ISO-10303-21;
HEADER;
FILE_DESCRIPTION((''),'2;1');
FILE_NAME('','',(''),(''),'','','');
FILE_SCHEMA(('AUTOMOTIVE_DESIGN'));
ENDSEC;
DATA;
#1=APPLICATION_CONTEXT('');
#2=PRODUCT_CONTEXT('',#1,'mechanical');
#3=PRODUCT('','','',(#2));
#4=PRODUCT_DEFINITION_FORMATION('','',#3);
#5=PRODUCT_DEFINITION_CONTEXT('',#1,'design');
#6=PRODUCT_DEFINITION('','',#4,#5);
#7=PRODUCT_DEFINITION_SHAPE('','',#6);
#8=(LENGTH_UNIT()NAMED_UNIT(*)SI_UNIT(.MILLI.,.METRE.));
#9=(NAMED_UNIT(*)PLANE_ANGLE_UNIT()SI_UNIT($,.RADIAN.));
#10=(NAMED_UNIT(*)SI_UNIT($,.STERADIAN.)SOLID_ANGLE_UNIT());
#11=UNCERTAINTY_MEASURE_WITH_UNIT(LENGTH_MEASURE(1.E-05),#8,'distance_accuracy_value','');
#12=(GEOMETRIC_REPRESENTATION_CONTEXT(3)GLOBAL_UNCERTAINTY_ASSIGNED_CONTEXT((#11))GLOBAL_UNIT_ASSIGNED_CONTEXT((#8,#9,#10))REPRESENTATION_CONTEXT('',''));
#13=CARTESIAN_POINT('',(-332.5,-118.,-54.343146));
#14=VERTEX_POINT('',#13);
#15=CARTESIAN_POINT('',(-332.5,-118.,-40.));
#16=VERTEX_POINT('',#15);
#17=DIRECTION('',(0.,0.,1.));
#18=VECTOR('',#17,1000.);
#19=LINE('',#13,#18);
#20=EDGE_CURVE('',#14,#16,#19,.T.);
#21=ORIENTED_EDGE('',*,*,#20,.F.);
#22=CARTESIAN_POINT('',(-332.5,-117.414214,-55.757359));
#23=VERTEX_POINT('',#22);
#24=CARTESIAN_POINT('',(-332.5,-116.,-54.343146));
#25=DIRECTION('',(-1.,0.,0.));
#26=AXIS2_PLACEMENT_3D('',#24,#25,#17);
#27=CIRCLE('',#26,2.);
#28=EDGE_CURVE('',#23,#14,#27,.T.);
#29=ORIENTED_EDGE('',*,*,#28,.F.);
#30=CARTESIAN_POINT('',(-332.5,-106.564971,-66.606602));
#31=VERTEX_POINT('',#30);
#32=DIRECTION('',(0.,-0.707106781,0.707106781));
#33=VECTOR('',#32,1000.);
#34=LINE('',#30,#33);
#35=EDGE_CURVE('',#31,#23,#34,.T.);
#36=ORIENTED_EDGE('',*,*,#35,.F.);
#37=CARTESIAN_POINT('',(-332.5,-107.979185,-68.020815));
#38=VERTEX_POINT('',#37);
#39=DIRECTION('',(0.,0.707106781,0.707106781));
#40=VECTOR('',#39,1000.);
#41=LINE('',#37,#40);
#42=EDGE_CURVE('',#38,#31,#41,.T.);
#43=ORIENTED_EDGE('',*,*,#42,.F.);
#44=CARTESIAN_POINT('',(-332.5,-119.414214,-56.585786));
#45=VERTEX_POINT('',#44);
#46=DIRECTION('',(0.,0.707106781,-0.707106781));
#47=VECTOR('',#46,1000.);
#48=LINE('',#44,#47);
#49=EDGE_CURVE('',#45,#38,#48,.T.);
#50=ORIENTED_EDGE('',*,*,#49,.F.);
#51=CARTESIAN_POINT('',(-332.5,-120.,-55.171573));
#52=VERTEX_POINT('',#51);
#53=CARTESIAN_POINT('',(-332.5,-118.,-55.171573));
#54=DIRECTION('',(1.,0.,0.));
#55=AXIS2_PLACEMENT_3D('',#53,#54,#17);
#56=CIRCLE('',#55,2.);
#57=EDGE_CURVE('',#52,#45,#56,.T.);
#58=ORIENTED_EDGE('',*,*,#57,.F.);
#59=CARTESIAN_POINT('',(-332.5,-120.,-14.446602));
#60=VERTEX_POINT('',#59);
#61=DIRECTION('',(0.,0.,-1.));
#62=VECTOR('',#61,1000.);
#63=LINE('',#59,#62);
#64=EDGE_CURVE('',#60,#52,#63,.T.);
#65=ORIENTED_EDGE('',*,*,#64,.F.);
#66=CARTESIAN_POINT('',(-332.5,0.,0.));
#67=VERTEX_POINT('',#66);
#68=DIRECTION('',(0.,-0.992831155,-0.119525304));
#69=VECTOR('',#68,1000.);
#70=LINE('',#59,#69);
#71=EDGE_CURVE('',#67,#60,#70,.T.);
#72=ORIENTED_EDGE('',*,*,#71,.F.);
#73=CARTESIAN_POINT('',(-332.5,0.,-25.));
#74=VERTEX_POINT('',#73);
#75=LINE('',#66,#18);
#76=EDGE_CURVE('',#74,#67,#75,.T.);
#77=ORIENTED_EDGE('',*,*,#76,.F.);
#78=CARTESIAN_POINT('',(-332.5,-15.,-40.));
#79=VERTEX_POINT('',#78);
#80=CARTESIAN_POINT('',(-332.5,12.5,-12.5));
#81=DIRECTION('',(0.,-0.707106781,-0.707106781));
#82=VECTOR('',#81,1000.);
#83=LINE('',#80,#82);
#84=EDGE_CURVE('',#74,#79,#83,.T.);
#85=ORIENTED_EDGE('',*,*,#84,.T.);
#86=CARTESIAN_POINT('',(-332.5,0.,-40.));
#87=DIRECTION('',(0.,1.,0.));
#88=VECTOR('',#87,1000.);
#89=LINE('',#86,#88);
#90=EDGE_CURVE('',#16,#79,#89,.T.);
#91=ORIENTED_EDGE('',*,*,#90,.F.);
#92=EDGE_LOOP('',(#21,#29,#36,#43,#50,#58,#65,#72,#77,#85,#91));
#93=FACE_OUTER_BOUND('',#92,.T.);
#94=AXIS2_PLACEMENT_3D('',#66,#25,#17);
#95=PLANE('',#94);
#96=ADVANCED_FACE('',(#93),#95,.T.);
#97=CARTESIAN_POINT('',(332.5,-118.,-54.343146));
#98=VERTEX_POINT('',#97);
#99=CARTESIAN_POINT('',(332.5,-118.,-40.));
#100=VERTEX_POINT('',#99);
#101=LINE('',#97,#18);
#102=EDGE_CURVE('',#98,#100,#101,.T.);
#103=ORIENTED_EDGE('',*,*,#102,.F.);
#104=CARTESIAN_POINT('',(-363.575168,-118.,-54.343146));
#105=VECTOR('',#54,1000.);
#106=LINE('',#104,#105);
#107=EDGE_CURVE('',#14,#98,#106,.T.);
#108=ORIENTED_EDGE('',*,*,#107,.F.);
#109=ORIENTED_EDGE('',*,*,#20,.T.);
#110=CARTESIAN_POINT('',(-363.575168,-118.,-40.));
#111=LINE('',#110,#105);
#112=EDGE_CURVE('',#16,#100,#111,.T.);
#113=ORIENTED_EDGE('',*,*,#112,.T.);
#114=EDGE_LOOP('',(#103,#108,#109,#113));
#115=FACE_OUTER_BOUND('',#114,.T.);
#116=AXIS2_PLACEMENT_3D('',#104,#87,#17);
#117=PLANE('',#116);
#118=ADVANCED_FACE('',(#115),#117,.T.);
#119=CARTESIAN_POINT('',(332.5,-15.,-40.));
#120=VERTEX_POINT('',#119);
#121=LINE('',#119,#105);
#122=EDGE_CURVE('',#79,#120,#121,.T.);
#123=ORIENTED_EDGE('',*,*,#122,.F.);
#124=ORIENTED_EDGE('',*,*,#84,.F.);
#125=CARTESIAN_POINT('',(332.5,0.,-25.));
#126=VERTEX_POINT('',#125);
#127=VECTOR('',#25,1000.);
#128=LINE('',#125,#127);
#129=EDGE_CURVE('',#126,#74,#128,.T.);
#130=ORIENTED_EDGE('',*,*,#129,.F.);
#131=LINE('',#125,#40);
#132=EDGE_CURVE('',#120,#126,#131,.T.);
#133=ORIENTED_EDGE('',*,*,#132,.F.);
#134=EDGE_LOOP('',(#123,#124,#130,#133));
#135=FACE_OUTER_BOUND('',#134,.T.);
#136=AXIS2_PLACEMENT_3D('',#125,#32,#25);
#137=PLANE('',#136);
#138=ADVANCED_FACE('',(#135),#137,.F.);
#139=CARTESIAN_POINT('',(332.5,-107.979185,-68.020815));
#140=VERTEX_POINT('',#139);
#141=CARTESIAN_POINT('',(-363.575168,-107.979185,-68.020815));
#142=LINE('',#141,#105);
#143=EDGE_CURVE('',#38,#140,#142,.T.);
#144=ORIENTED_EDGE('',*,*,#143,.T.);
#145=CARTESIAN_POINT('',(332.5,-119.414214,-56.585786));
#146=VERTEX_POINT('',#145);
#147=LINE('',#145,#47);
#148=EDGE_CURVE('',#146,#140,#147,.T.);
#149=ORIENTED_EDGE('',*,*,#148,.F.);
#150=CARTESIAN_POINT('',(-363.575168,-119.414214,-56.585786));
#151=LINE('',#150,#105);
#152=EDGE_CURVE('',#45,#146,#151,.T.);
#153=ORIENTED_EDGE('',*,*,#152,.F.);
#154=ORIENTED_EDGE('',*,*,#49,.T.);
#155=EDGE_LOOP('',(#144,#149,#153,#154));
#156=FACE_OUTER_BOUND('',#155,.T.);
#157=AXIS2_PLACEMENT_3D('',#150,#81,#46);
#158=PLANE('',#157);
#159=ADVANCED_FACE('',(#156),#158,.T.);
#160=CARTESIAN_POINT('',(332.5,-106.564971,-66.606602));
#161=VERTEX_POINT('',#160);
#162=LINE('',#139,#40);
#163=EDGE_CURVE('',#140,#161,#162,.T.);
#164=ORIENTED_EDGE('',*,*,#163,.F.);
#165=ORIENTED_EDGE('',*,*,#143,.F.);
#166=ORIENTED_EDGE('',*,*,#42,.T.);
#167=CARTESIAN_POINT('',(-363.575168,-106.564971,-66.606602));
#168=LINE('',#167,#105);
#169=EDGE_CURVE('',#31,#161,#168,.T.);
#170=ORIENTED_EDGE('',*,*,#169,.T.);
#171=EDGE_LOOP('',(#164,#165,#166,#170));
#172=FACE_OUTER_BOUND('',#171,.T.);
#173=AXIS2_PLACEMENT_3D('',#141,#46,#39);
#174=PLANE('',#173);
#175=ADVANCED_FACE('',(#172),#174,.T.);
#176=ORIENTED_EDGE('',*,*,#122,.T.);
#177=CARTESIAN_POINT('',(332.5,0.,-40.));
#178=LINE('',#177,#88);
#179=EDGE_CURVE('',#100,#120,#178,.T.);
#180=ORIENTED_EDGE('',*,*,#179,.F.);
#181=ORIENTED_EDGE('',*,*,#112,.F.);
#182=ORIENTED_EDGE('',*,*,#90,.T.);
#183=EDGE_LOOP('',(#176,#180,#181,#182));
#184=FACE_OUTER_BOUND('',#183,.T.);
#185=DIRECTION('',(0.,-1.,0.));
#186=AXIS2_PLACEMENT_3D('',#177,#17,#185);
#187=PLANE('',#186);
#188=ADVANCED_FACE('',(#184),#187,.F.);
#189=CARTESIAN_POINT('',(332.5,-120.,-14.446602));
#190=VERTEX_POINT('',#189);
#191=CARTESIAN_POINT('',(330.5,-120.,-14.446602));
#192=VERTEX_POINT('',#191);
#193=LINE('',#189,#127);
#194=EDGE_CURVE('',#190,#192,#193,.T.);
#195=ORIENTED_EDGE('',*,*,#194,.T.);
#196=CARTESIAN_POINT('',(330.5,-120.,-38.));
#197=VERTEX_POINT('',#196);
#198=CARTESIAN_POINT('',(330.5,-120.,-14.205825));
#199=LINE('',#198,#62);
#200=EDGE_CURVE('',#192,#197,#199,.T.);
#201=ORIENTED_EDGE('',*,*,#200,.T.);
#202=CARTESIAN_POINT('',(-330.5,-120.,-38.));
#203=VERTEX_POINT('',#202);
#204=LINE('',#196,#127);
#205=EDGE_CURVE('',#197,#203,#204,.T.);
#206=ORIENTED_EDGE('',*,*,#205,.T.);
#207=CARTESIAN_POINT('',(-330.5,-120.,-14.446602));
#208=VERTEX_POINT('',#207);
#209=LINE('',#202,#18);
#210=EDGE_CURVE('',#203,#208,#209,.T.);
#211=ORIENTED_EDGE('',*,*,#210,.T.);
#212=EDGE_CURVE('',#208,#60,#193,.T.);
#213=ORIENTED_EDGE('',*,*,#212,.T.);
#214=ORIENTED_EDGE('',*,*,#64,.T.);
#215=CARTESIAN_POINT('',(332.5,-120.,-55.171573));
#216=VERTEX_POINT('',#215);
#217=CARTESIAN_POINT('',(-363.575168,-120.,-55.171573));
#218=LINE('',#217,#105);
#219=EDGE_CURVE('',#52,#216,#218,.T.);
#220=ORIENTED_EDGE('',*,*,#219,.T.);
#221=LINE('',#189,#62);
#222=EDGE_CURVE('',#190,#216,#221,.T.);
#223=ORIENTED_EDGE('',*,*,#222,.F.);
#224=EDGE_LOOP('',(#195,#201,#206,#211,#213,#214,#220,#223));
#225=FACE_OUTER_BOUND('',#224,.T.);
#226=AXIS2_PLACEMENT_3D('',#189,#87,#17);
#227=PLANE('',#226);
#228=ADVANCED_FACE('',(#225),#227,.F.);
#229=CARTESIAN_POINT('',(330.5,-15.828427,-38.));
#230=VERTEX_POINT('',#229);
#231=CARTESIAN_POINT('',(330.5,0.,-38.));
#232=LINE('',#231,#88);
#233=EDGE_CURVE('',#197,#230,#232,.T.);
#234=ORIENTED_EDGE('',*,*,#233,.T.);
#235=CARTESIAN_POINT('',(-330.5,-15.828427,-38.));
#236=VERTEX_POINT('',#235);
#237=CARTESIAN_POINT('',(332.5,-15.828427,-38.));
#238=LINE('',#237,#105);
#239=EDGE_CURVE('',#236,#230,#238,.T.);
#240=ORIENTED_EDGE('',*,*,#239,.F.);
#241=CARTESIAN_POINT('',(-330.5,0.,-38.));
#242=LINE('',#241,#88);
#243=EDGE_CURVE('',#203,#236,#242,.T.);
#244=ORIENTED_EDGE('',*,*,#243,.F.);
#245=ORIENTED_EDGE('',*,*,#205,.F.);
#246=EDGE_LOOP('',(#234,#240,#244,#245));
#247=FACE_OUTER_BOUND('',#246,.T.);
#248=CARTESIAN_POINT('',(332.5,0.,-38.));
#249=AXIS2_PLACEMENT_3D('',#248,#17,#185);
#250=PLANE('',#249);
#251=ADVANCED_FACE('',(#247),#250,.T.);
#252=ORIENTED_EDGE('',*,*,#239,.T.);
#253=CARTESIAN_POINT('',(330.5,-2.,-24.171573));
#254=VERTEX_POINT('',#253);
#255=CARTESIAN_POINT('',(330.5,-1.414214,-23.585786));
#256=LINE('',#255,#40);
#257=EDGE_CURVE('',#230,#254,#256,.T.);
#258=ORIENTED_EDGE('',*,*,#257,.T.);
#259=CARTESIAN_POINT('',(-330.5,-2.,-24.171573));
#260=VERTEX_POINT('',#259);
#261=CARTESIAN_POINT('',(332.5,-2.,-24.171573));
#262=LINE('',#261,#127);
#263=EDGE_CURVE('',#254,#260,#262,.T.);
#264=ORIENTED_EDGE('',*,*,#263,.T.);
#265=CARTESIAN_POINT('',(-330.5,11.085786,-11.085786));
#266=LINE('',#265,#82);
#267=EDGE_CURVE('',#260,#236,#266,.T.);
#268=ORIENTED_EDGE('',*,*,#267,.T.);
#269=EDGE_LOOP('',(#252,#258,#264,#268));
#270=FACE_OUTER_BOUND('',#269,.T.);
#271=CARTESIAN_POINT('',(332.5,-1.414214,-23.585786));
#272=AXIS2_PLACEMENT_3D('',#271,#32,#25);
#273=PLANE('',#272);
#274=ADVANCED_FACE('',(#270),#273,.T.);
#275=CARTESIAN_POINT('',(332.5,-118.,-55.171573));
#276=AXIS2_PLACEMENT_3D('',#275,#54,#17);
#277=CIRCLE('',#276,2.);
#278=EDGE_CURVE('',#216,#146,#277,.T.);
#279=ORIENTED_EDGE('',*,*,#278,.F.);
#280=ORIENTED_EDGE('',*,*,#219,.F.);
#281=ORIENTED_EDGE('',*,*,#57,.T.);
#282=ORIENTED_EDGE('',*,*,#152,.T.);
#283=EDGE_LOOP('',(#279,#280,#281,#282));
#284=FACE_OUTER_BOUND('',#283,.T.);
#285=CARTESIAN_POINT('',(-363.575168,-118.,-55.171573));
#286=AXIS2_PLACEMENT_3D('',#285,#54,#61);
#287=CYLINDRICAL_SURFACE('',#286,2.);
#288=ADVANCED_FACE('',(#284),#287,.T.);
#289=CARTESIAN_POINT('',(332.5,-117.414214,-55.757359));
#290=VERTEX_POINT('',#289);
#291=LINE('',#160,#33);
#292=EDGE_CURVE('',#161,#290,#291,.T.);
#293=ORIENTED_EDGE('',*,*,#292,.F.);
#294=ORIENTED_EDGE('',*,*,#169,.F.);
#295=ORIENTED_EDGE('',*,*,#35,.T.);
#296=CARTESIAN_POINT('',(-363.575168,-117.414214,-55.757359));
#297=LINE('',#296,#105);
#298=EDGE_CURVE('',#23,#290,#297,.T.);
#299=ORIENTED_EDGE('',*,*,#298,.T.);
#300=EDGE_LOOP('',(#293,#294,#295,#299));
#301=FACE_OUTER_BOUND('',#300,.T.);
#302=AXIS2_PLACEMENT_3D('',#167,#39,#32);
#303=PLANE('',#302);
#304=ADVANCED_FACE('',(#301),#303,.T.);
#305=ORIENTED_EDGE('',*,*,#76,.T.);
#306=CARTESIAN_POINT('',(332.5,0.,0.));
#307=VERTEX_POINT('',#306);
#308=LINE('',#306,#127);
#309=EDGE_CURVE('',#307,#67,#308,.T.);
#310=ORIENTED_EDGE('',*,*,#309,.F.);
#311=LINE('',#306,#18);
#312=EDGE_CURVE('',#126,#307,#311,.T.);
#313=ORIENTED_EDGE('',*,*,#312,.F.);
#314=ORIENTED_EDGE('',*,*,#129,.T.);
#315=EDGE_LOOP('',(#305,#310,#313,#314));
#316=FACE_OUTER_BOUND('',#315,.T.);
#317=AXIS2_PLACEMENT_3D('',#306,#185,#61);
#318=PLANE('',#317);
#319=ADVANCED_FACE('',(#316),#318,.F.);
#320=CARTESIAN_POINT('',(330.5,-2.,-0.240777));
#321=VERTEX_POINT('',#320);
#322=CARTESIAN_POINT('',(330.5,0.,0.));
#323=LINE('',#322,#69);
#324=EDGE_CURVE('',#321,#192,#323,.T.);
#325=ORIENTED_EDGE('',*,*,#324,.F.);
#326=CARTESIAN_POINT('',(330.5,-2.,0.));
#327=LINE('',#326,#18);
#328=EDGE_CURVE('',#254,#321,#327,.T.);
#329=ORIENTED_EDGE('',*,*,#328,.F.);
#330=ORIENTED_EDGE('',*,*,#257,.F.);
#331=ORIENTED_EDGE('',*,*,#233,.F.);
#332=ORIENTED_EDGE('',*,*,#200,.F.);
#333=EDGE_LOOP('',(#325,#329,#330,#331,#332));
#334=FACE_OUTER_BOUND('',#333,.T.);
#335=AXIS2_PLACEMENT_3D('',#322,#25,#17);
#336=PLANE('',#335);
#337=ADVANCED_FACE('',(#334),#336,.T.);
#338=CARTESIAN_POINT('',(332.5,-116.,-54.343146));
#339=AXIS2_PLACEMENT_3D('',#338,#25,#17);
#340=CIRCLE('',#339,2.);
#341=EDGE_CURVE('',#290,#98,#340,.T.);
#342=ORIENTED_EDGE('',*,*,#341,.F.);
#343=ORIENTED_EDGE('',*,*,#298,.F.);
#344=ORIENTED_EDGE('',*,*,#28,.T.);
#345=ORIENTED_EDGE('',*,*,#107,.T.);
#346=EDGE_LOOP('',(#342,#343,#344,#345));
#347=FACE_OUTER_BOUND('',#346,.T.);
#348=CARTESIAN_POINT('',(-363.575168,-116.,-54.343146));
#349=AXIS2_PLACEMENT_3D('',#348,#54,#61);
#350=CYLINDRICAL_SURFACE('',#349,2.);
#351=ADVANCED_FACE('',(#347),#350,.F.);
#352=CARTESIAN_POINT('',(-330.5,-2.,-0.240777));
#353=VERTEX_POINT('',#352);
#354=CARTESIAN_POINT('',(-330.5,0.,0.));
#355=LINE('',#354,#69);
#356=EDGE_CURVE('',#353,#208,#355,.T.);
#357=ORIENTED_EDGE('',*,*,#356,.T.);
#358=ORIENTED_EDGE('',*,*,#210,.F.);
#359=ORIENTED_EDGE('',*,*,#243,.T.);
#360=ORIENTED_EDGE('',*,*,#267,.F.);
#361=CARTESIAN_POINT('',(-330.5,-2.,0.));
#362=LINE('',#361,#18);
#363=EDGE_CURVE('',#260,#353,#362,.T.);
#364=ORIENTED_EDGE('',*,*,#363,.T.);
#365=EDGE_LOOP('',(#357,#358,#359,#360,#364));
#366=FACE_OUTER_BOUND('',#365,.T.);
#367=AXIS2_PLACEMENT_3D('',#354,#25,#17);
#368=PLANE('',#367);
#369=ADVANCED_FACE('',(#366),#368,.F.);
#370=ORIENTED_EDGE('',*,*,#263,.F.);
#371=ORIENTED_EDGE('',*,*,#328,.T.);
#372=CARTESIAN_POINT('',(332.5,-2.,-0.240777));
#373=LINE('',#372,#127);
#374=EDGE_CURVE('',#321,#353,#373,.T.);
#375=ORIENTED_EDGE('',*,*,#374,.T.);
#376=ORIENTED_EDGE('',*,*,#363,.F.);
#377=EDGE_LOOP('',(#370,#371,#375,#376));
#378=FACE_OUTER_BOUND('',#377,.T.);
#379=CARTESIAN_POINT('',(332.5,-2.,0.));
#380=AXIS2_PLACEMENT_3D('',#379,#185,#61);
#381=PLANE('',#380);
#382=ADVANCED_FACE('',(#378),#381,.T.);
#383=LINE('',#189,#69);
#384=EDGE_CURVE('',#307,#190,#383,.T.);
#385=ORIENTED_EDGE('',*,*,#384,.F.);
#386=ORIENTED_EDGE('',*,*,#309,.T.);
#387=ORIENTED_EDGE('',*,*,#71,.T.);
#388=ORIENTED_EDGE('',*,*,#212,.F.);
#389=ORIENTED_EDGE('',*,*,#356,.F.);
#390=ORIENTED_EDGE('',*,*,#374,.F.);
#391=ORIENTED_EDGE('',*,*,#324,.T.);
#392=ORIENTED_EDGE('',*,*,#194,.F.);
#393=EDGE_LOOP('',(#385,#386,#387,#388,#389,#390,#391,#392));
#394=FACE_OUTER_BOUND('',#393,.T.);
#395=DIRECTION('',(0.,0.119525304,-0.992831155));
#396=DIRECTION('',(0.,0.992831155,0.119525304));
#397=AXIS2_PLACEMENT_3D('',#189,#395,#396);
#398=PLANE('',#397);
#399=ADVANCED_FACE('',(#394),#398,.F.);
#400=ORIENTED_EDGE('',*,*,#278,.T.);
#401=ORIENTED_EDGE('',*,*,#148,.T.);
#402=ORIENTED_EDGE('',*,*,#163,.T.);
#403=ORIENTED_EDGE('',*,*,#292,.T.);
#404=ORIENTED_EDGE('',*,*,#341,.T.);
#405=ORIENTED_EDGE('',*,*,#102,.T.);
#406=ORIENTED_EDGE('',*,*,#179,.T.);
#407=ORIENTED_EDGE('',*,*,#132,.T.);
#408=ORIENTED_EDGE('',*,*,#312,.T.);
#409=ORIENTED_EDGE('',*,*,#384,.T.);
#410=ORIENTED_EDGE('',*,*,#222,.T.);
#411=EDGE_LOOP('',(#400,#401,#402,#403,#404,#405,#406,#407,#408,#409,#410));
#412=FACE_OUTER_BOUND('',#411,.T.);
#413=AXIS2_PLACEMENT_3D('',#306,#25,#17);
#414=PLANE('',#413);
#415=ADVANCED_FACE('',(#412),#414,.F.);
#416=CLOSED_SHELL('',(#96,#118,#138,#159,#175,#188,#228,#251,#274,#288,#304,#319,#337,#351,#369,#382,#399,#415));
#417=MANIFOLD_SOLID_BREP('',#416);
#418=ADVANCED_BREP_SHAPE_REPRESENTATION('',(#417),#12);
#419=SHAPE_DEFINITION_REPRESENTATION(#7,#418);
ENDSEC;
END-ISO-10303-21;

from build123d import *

# Parameters (mm, degrees)
BOSS_EXTRUDE1_DEPTH = 332.5
CHAMFER1_SIZE       = 15
SHELL1_T            = -2
SKETCH7_W           = 661
SKETCH7_H           = 23.794174757
CUT_EXTRUDE1_DEPTH  = 356.077808374
BOSS_EXTRUDE2_DEPTH = 665


with BuildPart() as part:
    # Sketch1 → Boss-Extrude1 (new, symmetric)
    with BuildSketch(Plane(origin=(0, 0, 0), x_dir=(0, 0, -1), z_dir=(1, 0, 0))):
        Polygon((0, 0), (40, 0), (40, -120), (14.446601942, -120), align=None)
    extrude(amount=BOSS_EXTRUDE1_DEPTH, both=True)

    # Chamfer1
    chamfer1_edges = [part.edges().sort_by_distance(p)[0] for p in [
        (0, 0, -40),
    ]]
    chamfer(chamfer1_edges, length=CHAMFER1_SIZE)

    # Shell1
    shell1_openings = [part.faces().sort_by_distance(p)[0] for p in [
        (0, -60, -7.223300971),
    ]]
    offset(amount=SHELL1_T, openings=shell1_openings, kind=Kind.INTERSECTION)

    # Sketch7 → Cut-Extrude1 (cut, through all)
    with BuildSketch(Plane(origin=(0, -118, 0), x_dir=(1, 0, 0), z_dir=(0, 1, 0))):
        with Locations((0, 26.102912621)):
            Rectangle(SKETCH7_W, SKETCH7_H)
    extrude(amount=-CUT_EXTRUDE1_DEPTH, mode=Mode.SUBTRACT)

    # Sketch8 → Boss-Extrude2 (add)
    with BuildSketch(Plane(origin=(332.5, 0, 0), x_dir=(0, 0, -1), z_dir=(1, 0, 0))):
        with BuildLine():
            Line((40, -120), (55.171572875, -120))
            ThreePointArc((55.171572875, -120), (55.93693974, -119.847759065), (56.585786438, -119.414213562))
            Line((56.585786438, -119.414213562), (68.02081528, -107.97918472))
            Line((68.02081528, -107.97918472), (66.606601718, -106.564971157))
            Line((66.606601718, -106.564971157), (55.757359313, -117.414213562))
            ThreePointArc((55.757359313, -117.414213562), (55.108512615, -117.847759065), (54.343145751, -118))
            Line((54.343145751, -118), (40, -118))
            Line((40, -118), (40, -120))
        make_face()
    extrude(amount=-BOSS_EXTRUDE2_DEPTH)


solid = part.part
